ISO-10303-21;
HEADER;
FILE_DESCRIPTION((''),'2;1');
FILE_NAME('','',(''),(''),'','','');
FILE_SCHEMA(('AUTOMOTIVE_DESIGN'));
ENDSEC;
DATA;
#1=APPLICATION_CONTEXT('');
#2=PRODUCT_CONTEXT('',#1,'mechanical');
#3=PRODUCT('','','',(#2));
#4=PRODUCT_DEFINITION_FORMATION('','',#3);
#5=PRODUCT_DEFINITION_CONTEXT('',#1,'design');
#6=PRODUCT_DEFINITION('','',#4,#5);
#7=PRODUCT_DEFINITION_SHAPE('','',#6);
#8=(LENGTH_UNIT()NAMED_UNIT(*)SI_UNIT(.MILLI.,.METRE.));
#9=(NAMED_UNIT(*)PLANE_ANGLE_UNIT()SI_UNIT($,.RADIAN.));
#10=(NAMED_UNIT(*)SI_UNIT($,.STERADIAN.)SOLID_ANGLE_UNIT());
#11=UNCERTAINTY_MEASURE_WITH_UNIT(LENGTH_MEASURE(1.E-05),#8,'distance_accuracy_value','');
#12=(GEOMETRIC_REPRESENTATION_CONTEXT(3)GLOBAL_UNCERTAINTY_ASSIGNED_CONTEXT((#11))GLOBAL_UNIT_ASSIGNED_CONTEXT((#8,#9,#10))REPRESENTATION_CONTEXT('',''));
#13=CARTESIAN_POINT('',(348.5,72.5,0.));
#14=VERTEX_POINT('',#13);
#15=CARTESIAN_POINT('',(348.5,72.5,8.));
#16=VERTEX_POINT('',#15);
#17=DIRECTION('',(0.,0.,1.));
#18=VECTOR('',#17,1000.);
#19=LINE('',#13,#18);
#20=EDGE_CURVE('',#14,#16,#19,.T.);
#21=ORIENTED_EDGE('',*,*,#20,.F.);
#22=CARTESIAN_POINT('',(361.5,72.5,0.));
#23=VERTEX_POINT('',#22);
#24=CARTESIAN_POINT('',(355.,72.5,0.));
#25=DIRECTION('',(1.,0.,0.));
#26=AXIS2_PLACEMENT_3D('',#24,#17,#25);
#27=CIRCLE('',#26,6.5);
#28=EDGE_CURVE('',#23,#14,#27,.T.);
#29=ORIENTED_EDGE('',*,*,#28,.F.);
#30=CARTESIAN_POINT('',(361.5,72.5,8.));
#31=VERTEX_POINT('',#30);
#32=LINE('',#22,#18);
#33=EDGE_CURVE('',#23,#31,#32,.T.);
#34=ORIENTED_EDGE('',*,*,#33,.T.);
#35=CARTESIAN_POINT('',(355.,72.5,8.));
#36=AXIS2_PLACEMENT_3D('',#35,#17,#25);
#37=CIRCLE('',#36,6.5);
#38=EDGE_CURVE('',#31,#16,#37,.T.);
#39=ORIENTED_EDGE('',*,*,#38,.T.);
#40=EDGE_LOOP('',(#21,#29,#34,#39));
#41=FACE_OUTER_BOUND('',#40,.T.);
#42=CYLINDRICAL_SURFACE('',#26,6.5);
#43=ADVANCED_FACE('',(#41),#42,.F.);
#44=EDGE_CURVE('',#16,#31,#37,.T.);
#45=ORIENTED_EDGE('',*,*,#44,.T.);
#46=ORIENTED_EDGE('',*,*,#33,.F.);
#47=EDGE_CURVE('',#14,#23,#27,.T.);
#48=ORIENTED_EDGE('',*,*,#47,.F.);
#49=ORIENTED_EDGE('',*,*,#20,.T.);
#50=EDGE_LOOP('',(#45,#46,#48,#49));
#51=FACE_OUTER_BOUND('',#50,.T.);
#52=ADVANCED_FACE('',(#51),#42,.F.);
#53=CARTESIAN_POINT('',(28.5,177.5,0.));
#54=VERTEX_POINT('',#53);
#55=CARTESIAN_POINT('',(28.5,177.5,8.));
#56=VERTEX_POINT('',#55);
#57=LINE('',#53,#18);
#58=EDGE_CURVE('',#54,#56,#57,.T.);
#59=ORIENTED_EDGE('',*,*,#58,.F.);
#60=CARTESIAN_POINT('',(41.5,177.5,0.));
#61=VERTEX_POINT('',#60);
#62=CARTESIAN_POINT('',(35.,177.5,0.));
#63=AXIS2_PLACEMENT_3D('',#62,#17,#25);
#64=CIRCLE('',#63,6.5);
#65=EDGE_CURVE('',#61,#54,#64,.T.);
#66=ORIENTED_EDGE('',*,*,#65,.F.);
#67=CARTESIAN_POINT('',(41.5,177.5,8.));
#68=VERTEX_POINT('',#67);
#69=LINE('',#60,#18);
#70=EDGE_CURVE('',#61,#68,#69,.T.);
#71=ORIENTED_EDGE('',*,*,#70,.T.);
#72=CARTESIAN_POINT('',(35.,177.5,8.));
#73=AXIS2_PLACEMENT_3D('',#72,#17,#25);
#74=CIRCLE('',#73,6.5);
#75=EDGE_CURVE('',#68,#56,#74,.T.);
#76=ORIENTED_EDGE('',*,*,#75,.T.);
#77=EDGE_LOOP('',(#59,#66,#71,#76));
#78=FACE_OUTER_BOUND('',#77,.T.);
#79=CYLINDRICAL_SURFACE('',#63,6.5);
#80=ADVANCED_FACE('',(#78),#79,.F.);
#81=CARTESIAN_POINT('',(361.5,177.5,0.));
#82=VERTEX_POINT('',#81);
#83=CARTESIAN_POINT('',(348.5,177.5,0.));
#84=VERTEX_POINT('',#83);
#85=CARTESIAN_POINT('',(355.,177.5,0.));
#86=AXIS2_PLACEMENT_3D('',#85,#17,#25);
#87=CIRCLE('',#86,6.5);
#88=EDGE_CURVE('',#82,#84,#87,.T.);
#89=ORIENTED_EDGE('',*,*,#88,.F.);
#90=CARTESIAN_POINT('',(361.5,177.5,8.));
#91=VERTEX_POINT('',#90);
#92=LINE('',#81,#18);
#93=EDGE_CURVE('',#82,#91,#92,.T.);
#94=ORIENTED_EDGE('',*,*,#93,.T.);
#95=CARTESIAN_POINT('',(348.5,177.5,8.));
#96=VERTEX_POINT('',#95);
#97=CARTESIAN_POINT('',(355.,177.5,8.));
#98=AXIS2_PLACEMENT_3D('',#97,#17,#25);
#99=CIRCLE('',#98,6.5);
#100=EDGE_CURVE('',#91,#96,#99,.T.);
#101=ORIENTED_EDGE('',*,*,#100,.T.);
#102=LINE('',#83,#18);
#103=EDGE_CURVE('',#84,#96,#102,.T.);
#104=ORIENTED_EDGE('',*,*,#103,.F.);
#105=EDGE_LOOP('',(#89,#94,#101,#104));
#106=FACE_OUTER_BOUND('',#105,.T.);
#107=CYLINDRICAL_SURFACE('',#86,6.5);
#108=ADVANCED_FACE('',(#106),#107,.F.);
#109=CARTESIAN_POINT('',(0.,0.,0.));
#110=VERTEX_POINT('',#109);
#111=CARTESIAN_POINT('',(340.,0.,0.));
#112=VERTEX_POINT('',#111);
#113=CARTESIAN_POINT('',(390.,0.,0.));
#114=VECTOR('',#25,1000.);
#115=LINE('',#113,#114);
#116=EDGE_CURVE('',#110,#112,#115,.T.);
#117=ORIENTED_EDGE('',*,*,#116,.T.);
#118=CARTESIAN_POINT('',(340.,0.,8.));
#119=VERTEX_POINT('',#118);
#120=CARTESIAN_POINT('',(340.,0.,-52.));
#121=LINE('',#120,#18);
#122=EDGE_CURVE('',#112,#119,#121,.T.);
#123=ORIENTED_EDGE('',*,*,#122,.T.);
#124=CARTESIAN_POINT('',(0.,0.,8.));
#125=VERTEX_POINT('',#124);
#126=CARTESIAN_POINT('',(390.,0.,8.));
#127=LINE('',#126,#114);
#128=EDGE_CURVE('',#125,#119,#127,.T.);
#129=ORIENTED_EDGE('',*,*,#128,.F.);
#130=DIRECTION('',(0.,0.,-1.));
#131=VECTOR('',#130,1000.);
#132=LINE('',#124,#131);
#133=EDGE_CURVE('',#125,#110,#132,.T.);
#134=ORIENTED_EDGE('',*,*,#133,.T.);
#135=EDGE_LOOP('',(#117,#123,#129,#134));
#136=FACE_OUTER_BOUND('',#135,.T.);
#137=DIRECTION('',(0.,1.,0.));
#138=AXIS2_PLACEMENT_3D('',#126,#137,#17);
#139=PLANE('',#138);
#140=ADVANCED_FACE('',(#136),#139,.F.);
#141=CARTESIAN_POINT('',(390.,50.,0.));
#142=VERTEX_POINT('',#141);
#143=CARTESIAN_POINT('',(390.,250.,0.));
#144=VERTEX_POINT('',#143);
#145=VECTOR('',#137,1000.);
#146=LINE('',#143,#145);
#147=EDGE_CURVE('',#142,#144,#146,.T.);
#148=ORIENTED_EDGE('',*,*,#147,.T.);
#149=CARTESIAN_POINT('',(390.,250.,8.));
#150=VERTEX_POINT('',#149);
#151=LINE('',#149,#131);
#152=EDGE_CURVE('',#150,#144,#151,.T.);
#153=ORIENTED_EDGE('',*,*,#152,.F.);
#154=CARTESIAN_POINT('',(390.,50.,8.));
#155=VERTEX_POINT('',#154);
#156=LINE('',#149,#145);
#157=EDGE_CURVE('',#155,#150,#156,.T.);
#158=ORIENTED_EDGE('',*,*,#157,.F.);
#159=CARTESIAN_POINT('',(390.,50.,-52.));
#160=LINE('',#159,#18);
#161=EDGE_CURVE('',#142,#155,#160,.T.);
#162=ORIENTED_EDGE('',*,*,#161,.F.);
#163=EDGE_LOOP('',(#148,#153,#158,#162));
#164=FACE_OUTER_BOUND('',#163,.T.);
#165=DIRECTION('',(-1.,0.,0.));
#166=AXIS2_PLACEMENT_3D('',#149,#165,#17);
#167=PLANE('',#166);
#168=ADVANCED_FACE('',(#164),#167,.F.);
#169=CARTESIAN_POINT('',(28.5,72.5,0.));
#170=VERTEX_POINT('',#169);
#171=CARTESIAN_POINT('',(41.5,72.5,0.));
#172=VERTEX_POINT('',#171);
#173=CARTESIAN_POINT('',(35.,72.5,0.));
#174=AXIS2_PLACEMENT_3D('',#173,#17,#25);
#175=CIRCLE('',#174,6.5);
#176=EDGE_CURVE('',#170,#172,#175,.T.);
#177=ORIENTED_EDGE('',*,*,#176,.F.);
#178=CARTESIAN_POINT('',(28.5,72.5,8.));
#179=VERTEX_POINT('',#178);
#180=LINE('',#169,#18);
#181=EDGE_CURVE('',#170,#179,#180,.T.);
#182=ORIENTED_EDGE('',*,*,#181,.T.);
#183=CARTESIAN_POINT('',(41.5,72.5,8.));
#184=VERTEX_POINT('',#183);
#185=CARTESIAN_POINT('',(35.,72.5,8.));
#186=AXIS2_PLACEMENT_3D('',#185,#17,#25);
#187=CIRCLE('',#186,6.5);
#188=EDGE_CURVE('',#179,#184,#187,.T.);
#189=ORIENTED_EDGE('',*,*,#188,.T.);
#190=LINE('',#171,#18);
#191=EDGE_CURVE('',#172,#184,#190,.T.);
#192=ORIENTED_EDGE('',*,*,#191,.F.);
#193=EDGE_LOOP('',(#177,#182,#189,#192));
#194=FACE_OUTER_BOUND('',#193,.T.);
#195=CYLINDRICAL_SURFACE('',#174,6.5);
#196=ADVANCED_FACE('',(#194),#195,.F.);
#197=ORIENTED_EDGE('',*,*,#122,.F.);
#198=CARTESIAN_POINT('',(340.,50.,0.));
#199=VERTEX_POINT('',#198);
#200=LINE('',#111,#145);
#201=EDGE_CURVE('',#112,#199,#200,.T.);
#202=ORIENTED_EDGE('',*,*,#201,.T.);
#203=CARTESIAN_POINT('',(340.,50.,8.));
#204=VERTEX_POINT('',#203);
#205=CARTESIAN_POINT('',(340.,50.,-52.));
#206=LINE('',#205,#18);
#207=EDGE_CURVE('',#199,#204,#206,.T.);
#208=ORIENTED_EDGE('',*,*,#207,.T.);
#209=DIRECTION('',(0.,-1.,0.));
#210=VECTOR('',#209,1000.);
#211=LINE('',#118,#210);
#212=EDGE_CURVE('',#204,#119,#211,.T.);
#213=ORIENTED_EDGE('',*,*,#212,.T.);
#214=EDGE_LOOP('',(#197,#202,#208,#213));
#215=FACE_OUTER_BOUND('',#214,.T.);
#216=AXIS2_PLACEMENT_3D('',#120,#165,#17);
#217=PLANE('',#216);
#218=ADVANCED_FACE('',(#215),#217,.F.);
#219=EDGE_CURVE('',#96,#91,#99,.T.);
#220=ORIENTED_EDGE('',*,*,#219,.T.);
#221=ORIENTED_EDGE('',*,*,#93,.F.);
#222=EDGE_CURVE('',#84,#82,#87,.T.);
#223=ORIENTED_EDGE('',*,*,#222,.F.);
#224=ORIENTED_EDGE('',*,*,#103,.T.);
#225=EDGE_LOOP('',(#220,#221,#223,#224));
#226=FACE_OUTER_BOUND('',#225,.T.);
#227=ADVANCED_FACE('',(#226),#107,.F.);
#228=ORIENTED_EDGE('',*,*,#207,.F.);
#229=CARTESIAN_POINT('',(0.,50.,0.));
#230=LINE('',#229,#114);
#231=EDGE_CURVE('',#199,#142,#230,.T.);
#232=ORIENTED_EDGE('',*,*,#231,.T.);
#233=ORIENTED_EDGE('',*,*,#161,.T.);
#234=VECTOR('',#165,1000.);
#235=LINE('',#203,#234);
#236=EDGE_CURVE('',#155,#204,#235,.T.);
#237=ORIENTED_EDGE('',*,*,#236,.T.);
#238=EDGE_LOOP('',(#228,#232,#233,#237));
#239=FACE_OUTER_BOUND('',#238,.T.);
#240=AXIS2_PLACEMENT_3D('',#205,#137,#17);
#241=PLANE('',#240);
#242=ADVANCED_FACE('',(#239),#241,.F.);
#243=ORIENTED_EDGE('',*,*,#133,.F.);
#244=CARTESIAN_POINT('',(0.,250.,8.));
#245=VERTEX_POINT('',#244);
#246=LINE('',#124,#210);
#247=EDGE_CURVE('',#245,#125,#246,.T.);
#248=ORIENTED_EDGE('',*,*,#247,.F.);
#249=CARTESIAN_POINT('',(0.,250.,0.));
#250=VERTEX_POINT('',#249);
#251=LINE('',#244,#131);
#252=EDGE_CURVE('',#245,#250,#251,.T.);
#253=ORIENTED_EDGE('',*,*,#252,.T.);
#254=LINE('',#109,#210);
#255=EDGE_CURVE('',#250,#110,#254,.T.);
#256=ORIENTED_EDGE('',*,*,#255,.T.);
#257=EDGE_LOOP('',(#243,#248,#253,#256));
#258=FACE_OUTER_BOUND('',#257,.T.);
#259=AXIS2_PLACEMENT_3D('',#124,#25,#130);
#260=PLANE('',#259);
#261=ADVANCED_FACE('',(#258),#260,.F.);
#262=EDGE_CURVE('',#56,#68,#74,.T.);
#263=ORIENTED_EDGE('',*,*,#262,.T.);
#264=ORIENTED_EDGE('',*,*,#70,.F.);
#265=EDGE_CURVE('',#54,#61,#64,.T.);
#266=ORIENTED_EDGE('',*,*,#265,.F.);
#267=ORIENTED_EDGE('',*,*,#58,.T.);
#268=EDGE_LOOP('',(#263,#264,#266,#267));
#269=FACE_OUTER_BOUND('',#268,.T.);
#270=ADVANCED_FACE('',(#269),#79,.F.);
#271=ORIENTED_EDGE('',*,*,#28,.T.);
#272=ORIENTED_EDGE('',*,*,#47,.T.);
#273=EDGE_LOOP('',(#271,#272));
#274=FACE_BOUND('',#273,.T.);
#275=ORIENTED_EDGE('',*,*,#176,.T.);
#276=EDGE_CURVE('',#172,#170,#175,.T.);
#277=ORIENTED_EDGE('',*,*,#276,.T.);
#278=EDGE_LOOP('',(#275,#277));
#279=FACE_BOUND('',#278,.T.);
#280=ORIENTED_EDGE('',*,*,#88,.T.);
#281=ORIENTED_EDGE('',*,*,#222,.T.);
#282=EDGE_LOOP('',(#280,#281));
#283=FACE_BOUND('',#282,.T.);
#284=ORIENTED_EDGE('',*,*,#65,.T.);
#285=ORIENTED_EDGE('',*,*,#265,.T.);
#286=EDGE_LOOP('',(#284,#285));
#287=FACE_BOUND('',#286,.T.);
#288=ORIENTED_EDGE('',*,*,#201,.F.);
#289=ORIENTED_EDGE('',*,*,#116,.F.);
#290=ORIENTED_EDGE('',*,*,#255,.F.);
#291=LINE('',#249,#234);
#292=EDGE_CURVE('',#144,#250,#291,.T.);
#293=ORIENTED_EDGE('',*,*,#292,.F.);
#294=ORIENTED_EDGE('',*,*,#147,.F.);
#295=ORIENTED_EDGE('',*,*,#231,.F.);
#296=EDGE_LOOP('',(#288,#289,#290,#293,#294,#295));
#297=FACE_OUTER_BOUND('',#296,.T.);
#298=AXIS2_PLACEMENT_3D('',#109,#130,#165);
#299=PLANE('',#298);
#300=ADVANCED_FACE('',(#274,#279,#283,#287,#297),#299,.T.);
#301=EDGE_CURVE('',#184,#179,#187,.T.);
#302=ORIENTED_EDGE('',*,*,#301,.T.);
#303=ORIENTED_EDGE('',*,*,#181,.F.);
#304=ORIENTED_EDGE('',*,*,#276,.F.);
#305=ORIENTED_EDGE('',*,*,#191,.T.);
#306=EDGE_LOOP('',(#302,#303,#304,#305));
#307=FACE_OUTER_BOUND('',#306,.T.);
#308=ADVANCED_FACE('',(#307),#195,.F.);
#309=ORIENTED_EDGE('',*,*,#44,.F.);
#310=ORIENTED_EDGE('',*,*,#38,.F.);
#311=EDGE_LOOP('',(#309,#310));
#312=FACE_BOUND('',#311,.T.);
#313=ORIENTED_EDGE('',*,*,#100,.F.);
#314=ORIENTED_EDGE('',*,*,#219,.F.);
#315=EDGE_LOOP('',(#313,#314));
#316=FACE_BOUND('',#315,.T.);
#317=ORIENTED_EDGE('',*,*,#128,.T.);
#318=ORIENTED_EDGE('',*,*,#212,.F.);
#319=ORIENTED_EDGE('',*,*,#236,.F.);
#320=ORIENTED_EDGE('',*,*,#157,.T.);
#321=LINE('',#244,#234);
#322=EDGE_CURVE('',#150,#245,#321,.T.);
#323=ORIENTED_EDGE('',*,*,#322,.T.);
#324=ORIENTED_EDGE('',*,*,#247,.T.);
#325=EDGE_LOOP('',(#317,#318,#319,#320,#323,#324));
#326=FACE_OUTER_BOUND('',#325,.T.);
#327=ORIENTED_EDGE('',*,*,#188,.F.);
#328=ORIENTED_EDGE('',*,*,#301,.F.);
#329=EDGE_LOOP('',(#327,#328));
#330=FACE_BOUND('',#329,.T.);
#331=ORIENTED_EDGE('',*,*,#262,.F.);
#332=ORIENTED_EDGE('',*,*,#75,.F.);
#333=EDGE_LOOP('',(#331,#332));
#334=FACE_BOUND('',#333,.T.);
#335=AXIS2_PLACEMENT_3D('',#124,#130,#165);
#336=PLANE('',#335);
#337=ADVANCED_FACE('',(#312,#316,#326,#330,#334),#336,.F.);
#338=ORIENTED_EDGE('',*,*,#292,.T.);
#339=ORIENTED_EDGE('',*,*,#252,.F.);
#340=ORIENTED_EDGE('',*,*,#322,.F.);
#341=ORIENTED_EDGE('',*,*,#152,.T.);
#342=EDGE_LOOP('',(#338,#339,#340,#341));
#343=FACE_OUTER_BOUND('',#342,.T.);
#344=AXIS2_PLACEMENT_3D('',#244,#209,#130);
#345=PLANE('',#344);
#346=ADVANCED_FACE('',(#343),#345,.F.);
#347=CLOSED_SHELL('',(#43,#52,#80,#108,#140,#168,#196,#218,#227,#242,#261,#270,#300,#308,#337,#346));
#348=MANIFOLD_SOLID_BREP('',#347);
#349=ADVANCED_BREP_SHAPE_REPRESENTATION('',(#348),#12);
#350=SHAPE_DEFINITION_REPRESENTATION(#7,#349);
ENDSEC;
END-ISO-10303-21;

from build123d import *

# Parameters (mm, degrees)
SKETCH_1_W          = 390
SKETCH_1_H          = 250
EXTRUDE_1_DEPTH     = 8
CUT_EXTRUDE_1_DEPTH = 8
SKETCH_3_W          = 50
SKETCH_3_H          = 50
CUT_EXTRUDE_2_DEPTH = 60


with BuildPart() as part:
    # 草图1 → 凸台-拉伸1 (new body)
    with BuildSketch(Plane.XY):
        with Locations((195, 125)):
            Rectangle(SKETCH_1_W, SKETCH_1_H)
    extrude(amount=EXTRUDE_1_DEPTH)

    # 草图2 → 切除-拉伸1 (cut)
    with BuildSketch(Plane.XY.offset(8)):
        with BuildLine():
            ThreePointArc((41.5, 177.5), (30.403805922, 182.096194078), (35, 171))
            Line((35, 171), (35, 177.5))
            Line((35, 177.5), (41.5, 177.5))
        make_face()
        with BuildLine():
            Line((35, 177.5), (35, 171))
            ThreePointArc((35, 171), (39.596194078, 172.903805922), (41.5, 177.5))
            Line((41.5, 177.5), (35, 177.5))
        make_face()
        with BuildLine():
            Line((35, 79), (35, 72.5))
            Line((35, 72.5), (41.5, 72.5))
            ThreePointArc((41.5, 72.5), (39.596194078, 77.096194078), (35, 79))
        make_face()
        with BuildLine():
            Line((41.5, 72.5), (35, 72.5))
            Line((35, 72.5), (35, 79))
            ThreePointArc((35, 79), (30.403805922, 67.903805922), (41.5, 72.5))
        make_face()
        with BuildLine():
            ThreePointArc((355, 79), (350.403805922, 77.096194078), (348.5, 72.5))
            Line((348.5, 72.5), (355, 72.5))
            Line((355, 72.5), (355, 79))
        make_face()
        with BuildLine():
            Line((355, 72.5), (348.5, 72.5))
            ThreePointArc((348.5, 72.5), (355, 66), (361.5, 72.5))
            ThreePointArc((361.5, 72.5), (359.596194078, 77.096194078), (355, 79))
            Line((355, 79), (355, 72.5))
        make_face()
        with BuildLine():
            ThreePointArc((348.5, 177.5), (350.403805922, 172.903805922), (355, 171))
            Line((355, 171), (355, 177.5))
            Line((355, 177.5), (348.5, 177.5))
        make_face()
        with BuildLine():
            Line((355, 177.5), (355, 171))
            ThreePointArc((355, 171), (359.596194078, 172.903805922), (361.5, 177.5))
            ThreePointArc((361.5, 177.5), (355, 184), (348.5, 177.5))
            Line((348.5, 177.5), (355, 177.5))
        make_face()
    extrude(amount=-CUT_EXTRUDE_1_DEPTH, mode=Mode.SUBTRACT)

    # 草图3 → 切除-拉伸2 (cut)
    with BuildSketch(Plane.XY.offset(8)):
        with Locations((365, 25)):
            Rectangle(SKETCH_3_W, SKETCH_3_H)
    extrude(amount=-CUT_EXTRUDE_2_DEPTH, mode=Mode.SUBTRACT)


solid = part.part
